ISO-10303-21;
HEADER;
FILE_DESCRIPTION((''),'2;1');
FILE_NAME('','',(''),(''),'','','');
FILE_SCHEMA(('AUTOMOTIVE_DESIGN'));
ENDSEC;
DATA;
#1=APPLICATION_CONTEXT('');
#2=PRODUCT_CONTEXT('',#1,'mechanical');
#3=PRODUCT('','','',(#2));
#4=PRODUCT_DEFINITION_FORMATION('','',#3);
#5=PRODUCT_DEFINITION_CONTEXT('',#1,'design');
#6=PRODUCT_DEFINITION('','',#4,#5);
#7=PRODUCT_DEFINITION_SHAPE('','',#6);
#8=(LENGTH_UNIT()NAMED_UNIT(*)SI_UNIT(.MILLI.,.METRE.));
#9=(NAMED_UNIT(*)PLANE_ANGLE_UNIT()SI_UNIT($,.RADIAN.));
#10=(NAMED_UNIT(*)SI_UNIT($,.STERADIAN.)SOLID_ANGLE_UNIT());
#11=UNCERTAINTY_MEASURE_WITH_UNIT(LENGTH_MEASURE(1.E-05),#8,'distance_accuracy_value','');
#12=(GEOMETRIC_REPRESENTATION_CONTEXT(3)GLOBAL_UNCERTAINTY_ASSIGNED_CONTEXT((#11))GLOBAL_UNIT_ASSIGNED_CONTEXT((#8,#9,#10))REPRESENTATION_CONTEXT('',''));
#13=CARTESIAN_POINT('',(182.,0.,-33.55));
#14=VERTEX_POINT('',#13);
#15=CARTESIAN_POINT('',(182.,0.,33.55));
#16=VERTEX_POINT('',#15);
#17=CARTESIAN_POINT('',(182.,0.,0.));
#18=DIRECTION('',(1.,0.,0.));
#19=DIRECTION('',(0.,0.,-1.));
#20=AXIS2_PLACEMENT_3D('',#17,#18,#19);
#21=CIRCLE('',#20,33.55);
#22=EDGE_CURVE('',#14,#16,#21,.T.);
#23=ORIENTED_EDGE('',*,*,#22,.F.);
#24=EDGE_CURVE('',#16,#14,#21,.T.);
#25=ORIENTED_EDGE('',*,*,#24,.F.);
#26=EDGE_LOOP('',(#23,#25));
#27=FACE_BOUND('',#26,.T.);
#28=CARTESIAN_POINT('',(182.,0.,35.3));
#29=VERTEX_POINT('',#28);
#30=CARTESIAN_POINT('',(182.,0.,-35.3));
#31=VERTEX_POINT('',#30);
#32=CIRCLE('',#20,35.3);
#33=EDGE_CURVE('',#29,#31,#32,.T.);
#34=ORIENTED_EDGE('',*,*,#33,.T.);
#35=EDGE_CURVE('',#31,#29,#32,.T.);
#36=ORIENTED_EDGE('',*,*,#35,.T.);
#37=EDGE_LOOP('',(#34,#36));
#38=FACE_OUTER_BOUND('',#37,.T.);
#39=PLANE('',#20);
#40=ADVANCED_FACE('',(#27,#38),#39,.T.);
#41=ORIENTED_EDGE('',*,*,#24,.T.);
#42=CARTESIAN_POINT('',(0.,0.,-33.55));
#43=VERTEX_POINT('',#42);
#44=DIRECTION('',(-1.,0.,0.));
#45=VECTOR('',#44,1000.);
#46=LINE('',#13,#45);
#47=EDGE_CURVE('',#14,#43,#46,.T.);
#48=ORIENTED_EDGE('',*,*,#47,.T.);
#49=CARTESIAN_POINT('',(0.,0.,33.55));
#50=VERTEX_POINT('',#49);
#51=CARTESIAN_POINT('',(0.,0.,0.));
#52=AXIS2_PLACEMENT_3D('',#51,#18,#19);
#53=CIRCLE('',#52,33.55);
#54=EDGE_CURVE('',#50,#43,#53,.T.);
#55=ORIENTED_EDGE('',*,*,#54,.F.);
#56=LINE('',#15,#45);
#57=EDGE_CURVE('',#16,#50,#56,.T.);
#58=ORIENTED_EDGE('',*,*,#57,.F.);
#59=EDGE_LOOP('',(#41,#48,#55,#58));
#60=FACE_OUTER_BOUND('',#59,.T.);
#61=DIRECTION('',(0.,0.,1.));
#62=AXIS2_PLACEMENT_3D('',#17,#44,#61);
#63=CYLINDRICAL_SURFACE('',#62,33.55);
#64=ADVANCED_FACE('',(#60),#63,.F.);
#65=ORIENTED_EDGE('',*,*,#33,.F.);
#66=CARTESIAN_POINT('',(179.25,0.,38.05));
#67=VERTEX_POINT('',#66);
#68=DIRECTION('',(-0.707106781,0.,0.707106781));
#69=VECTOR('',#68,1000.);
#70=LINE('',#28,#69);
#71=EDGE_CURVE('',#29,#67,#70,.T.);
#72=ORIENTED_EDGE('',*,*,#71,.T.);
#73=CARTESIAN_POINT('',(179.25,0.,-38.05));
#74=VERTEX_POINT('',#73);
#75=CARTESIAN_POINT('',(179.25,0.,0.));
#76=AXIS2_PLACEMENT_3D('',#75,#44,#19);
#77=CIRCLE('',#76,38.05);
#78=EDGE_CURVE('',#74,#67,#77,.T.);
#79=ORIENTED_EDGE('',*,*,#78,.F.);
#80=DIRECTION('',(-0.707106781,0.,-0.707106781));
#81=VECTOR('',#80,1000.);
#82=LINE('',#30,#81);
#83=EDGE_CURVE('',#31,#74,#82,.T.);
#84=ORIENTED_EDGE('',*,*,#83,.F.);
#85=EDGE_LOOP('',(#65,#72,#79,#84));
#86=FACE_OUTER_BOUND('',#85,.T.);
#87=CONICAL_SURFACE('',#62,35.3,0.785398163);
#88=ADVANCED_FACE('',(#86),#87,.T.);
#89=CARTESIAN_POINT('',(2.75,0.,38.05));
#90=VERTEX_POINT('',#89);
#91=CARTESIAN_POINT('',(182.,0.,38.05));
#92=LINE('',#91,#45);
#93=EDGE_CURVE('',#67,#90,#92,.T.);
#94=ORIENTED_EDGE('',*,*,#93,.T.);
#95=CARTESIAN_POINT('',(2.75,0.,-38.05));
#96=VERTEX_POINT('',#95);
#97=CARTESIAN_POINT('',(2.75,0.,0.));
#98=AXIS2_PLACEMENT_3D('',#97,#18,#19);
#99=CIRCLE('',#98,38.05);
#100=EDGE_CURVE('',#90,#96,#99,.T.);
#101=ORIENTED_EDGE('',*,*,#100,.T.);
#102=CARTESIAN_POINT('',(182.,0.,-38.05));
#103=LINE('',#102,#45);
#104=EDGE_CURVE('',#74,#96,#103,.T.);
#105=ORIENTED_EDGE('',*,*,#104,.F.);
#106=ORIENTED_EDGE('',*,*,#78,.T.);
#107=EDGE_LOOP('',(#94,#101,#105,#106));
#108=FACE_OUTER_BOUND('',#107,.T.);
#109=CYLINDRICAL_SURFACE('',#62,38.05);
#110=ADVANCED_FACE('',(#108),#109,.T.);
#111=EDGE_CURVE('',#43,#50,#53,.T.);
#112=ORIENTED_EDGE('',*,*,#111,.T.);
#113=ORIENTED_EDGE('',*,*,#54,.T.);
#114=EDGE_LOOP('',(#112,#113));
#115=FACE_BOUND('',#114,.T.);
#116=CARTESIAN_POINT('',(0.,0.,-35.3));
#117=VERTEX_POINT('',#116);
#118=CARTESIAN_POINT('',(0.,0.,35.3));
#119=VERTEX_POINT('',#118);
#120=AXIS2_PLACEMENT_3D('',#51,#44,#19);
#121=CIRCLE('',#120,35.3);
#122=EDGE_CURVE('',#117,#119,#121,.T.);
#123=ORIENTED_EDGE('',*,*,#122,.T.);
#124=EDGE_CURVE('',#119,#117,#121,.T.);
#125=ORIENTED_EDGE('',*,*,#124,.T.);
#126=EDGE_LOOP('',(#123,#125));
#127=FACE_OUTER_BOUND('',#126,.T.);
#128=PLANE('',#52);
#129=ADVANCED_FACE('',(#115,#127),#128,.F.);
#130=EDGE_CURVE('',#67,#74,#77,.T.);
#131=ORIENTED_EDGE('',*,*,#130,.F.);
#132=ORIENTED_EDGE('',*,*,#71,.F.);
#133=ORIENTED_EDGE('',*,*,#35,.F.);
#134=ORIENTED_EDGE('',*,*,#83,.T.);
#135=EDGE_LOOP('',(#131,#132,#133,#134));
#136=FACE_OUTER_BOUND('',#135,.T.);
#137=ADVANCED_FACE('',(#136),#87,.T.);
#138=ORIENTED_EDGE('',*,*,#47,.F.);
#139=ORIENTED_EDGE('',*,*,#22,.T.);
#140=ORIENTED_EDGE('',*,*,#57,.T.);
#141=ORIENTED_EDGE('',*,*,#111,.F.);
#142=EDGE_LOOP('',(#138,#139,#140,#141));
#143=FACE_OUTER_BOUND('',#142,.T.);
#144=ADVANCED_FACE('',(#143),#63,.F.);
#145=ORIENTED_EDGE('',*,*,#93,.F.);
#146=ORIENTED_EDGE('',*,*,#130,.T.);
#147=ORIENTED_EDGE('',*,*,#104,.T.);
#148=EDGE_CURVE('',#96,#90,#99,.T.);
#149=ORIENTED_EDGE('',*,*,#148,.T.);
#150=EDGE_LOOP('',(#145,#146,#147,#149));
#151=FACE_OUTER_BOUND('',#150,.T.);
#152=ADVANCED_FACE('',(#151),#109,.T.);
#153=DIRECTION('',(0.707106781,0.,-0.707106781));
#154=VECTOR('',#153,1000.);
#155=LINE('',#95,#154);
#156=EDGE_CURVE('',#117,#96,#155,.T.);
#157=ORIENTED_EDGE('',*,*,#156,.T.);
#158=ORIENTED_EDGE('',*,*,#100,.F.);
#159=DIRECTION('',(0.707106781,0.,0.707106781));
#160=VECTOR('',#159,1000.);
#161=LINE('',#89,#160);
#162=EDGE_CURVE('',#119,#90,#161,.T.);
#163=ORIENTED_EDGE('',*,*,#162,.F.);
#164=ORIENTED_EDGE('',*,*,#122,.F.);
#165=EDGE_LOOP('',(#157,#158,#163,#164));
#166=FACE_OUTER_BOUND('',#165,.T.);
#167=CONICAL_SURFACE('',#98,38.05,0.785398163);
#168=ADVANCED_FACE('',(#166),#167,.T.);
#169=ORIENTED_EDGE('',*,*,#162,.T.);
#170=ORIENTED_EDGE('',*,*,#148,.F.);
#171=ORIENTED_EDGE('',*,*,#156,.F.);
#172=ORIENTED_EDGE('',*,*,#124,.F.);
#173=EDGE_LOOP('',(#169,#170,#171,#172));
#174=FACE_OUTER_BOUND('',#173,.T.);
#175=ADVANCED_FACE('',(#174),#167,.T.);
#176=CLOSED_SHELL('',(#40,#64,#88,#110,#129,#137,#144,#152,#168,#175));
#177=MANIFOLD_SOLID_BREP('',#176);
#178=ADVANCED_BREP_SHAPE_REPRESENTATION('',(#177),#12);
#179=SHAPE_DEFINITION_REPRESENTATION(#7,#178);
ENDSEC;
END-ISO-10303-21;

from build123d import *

# Parameters (mm, degrees)
SKETCH1_R                      = 38.05
SKETCH1_R_2                    = 33.55
GB_T3091_2008_76_1X4_5_1_DEPTH = 182
CHAMFER_1_SIZE                 = 2.75


with BuildPart() as part:
    # Sketch1 → 焊接钢管gb∕t3091-2008 Φ76.1X4.5(1) (new body)
    with BuildSketch(Plane.YZ):
        Circle(SKETCH1_R)
        Circle(SKETCH1_R_2, mode=Mode.SUBTRACT)
    extrude(amount=GB_T3091_2008_76_1X4_5_1_DEPTH)

    # 倒角1
    chamfer_1_edges = [part.edges().sort_by_distance(p)[0] for p in [
        (182, -38.05, 0),
        (0, -38.05, 0),
    ]]
    chamfer(chamfer_1_edges, length=CHAMFER_1_SIZE)


solid = part.part
